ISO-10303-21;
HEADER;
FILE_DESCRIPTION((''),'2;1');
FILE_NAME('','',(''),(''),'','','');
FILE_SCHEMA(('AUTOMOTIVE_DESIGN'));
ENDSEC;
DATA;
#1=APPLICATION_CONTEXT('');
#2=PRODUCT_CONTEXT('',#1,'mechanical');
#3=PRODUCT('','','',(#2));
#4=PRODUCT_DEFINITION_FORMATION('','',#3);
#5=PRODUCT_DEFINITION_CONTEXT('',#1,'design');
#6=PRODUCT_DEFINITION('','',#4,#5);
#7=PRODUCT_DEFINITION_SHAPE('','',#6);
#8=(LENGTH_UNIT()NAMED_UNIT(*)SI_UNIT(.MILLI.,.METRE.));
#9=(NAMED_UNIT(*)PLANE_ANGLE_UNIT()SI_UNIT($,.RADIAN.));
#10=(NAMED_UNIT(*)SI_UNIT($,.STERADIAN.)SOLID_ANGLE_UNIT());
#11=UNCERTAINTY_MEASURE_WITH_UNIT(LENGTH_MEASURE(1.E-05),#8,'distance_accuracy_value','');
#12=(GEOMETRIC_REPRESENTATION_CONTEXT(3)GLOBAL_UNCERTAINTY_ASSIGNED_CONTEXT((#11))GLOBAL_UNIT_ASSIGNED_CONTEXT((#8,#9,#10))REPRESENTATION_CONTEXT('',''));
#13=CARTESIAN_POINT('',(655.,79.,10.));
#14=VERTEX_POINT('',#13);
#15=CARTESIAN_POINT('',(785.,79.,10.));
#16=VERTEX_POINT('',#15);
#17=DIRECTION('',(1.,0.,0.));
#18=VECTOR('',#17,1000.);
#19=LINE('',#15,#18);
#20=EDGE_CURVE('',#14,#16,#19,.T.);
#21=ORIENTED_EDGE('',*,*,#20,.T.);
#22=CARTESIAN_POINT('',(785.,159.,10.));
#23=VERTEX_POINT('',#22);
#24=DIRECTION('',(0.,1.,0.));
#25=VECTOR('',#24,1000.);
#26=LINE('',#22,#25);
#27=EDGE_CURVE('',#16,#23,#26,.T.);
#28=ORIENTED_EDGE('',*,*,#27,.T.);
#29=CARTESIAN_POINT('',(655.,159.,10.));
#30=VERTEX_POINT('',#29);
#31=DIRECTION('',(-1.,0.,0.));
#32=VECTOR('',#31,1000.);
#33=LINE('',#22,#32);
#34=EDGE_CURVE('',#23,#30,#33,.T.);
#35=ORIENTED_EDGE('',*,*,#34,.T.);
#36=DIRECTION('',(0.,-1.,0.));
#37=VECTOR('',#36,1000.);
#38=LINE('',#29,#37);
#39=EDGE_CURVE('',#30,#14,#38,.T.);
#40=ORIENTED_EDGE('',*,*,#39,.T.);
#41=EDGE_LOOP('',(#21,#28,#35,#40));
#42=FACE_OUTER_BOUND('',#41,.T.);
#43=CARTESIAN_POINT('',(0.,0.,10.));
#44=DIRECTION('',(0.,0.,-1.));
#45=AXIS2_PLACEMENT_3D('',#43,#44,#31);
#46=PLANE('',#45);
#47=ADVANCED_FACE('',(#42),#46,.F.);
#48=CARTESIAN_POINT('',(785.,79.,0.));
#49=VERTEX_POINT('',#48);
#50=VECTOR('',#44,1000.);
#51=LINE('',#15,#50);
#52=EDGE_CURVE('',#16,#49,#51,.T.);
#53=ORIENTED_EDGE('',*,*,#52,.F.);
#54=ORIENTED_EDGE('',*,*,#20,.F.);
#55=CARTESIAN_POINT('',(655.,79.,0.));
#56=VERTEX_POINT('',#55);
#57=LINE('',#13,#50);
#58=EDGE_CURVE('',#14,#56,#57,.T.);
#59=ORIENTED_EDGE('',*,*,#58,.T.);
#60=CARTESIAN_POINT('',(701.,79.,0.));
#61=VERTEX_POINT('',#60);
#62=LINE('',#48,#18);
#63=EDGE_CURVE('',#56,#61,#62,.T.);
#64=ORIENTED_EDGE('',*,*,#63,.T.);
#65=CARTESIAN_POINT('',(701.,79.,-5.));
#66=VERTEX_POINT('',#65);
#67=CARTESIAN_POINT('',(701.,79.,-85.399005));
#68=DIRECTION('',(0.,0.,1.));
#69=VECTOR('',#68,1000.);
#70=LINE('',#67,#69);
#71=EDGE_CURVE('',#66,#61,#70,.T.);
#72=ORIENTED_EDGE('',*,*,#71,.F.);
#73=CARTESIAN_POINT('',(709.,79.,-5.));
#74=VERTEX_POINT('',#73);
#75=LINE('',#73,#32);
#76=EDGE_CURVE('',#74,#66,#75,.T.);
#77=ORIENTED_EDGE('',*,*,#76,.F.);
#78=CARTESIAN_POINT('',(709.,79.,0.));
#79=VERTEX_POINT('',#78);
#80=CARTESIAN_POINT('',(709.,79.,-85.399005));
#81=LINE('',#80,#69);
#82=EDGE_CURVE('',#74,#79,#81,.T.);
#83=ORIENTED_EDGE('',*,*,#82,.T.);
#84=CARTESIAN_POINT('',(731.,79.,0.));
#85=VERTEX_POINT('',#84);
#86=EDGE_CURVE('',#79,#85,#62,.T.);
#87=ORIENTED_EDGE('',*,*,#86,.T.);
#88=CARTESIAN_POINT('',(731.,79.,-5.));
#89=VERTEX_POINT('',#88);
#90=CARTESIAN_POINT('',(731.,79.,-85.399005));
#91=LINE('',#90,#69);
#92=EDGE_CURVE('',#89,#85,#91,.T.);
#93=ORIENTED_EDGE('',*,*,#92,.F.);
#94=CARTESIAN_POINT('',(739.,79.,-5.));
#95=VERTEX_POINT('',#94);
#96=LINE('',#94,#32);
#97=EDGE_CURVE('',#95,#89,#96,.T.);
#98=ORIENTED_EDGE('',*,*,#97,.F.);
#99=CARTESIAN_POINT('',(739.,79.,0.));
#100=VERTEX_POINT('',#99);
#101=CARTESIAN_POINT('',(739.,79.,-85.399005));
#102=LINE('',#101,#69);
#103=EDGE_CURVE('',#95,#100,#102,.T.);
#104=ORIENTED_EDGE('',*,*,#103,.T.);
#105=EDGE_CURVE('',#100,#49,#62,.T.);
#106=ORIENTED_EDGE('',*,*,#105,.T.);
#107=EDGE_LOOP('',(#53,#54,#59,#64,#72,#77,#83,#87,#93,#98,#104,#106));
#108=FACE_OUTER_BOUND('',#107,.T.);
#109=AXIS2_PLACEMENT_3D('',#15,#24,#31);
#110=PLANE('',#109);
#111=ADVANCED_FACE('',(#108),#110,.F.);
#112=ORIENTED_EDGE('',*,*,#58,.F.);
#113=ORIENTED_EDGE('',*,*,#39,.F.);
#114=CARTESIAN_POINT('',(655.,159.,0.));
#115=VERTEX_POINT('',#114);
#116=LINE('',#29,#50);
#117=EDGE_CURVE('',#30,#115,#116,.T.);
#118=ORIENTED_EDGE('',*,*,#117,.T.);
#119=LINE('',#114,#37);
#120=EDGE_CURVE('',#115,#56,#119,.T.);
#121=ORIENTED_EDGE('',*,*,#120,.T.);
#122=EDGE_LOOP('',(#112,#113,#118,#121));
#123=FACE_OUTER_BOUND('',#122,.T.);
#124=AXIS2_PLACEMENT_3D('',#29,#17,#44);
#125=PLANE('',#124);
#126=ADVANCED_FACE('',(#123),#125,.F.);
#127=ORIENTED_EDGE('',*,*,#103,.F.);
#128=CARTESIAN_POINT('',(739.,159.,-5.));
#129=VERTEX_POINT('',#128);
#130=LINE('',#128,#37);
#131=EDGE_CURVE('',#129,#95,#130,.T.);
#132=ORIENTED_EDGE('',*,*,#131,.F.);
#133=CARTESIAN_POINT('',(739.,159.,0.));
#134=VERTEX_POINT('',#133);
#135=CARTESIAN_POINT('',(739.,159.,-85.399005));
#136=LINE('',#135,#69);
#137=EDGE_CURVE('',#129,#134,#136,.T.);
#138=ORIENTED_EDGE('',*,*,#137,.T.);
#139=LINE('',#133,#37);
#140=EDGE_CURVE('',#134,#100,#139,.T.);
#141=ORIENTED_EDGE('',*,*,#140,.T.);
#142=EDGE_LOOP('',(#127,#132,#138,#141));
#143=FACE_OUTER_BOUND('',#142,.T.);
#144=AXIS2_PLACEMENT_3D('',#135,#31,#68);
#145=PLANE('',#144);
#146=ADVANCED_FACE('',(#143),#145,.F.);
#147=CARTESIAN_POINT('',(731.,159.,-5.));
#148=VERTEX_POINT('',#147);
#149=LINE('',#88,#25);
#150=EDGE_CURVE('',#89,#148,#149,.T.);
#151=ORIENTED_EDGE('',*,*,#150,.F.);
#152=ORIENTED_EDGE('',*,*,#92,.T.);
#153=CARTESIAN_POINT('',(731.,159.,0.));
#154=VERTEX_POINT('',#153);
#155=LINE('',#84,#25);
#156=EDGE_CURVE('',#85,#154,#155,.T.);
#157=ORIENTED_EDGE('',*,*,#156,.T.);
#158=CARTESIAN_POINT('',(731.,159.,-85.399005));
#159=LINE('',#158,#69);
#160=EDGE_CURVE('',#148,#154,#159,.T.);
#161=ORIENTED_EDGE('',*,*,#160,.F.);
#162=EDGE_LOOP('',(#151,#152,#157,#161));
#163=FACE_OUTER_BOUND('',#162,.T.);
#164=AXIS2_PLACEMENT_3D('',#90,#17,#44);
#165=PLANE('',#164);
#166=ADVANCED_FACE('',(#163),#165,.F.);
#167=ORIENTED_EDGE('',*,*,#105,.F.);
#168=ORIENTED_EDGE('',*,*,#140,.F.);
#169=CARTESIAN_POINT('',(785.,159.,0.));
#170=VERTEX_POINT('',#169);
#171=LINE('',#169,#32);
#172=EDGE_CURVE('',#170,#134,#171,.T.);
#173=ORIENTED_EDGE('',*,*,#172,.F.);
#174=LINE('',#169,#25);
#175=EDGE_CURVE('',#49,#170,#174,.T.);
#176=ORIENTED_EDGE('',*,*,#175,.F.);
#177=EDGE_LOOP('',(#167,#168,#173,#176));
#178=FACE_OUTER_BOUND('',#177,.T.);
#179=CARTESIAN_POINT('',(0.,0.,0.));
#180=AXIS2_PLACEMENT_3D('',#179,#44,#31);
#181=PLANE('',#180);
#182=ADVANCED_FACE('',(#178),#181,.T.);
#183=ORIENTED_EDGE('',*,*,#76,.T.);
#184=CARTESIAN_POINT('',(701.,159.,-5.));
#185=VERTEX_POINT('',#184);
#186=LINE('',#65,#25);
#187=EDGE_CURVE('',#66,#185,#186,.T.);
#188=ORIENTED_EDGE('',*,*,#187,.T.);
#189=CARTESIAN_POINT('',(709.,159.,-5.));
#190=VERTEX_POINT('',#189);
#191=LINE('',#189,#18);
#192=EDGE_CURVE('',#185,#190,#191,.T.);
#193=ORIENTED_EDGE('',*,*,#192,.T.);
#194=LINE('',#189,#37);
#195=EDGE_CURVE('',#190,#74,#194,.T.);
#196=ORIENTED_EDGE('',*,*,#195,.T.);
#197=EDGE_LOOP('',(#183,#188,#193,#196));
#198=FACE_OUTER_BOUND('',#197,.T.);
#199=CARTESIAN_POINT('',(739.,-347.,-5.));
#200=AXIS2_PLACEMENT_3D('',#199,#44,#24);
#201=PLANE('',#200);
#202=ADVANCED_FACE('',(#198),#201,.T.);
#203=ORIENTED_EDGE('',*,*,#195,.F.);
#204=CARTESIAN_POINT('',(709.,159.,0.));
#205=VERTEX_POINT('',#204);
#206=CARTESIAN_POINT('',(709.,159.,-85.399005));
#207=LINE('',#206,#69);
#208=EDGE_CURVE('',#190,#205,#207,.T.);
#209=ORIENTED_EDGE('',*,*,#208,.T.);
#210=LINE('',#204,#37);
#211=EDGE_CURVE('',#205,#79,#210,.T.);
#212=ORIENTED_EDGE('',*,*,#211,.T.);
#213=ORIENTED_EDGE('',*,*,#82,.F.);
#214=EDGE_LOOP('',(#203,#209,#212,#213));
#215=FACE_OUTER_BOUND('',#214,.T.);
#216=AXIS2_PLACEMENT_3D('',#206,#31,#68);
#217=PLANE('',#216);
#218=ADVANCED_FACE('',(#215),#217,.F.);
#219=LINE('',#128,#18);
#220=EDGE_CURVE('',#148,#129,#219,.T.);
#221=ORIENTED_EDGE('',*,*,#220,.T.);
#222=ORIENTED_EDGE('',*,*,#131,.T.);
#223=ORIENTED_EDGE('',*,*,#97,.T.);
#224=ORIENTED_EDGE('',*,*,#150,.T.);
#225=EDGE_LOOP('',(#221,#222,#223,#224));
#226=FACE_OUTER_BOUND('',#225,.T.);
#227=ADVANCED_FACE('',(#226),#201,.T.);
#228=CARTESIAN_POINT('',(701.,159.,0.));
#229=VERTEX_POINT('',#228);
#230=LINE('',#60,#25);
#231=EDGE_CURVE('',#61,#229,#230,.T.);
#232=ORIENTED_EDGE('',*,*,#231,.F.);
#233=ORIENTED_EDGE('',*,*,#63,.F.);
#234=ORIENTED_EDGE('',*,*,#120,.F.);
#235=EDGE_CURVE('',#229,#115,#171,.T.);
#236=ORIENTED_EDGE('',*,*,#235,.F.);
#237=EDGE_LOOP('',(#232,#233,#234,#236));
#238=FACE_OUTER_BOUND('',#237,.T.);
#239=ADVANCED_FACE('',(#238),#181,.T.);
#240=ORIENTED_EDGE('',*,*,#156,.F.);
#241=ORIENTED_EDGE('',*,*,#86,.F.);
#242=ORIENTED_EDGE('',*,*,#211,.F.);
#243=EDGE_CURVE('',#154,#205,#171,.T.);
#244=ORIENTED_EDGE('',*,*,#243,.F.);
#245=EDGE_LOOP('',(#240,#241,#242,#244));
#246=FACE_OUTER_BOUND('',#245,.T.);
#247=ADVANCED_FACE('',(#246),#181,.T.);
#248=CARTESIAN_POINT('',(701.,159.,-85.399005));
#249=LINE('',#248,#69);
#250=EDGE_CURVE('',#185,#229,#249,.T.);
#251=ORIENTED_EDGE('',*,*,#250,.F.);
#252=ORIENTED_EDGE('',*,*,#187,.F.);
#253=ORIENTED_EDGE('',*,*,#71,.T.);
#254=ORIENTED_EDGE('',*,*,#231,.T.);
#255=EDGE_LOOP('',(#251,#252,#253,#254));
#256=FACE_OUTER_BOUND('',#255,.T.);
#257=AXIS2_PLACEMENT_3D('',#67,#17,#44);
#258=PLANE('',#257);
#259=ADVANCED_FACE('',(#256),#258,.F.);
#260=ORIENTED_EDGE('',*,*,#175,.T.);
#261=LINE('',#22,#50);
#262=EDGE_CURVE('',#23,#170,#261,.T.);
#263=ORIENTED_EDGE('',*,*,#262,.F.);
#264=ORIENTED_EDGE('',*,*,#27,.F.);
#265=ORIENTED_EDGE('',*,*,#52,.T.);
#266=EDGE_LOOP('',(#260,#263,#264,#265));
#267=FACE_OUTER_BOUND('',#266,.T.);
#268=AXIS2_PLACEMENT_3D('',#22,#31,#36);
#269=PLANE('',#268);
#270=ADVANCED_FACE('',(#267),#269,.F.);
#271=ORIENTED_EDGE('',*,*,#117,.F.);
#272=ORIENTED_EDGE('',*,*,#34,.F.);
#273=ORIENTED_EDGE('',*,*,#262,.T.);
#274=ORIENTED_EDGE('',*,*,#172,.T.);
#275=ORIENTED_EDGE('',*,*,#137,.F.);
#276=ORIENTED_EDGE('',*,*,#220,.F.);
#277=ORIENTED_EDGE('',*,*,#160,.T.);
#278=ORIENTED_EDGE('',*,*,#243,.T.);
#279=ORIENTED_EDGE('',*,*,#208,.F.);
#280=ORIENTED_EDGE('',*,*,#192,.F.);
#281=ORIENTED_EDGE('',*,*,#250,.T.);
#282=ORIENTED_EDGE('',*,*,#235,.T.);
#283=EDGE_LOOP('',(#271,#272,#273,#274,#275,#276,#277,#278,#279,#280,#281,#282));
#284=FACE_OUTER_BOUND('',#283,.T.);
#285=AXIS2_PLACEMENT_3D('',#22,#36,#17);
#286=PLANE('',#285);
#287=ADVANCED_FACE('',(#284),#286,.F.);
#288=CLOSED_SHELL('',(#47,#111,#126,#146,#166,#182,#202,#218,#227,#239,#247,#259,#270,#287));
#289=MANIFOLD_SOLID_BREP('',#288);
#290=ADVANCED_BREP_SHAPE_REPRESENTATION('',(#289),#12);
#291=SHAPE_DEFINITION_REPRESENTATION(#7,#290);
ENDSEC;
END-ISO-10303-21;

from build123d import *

# Parameters (mm, degrees)
SKETCH3_W           = 130
SKETCH3_H           = 80
BOSS_EXTRUDE1_DEPTH = 10
SKETCH4_W           = 8
SKETCH4_H           = 80
BOSS_EXTRUDE2_DEPTH = 5


with BuildPart() as part:
    # Sketch3 → Boss-Extrude1 (new body)
    with BuildSketch(Plane.XY):
        with Locations((720, 119)):
            Rectangle(SKETCH3_W, SKETCH3_H)
    extrude(amount=BOSS_EXTRUDE1_DEPTH)

    # Sketch4 → Boss-Extrude2 (add)
    with BuildSketch(Plane(origin=(0, 0, 0), x_dir=(-1, 0, 0), z_dir=(0, 0, -1))):
        with Locations((-735, 119)):
            Rectangle(SKETCH4_W, SKETCH4_H)
        with Locations((-705, 119)):
            Rectangle(SKETCH4_W, SKETCH4_H)
    extrude(amount=BOSS_EXTRUDE2_DEPTH)


solid = part.part
